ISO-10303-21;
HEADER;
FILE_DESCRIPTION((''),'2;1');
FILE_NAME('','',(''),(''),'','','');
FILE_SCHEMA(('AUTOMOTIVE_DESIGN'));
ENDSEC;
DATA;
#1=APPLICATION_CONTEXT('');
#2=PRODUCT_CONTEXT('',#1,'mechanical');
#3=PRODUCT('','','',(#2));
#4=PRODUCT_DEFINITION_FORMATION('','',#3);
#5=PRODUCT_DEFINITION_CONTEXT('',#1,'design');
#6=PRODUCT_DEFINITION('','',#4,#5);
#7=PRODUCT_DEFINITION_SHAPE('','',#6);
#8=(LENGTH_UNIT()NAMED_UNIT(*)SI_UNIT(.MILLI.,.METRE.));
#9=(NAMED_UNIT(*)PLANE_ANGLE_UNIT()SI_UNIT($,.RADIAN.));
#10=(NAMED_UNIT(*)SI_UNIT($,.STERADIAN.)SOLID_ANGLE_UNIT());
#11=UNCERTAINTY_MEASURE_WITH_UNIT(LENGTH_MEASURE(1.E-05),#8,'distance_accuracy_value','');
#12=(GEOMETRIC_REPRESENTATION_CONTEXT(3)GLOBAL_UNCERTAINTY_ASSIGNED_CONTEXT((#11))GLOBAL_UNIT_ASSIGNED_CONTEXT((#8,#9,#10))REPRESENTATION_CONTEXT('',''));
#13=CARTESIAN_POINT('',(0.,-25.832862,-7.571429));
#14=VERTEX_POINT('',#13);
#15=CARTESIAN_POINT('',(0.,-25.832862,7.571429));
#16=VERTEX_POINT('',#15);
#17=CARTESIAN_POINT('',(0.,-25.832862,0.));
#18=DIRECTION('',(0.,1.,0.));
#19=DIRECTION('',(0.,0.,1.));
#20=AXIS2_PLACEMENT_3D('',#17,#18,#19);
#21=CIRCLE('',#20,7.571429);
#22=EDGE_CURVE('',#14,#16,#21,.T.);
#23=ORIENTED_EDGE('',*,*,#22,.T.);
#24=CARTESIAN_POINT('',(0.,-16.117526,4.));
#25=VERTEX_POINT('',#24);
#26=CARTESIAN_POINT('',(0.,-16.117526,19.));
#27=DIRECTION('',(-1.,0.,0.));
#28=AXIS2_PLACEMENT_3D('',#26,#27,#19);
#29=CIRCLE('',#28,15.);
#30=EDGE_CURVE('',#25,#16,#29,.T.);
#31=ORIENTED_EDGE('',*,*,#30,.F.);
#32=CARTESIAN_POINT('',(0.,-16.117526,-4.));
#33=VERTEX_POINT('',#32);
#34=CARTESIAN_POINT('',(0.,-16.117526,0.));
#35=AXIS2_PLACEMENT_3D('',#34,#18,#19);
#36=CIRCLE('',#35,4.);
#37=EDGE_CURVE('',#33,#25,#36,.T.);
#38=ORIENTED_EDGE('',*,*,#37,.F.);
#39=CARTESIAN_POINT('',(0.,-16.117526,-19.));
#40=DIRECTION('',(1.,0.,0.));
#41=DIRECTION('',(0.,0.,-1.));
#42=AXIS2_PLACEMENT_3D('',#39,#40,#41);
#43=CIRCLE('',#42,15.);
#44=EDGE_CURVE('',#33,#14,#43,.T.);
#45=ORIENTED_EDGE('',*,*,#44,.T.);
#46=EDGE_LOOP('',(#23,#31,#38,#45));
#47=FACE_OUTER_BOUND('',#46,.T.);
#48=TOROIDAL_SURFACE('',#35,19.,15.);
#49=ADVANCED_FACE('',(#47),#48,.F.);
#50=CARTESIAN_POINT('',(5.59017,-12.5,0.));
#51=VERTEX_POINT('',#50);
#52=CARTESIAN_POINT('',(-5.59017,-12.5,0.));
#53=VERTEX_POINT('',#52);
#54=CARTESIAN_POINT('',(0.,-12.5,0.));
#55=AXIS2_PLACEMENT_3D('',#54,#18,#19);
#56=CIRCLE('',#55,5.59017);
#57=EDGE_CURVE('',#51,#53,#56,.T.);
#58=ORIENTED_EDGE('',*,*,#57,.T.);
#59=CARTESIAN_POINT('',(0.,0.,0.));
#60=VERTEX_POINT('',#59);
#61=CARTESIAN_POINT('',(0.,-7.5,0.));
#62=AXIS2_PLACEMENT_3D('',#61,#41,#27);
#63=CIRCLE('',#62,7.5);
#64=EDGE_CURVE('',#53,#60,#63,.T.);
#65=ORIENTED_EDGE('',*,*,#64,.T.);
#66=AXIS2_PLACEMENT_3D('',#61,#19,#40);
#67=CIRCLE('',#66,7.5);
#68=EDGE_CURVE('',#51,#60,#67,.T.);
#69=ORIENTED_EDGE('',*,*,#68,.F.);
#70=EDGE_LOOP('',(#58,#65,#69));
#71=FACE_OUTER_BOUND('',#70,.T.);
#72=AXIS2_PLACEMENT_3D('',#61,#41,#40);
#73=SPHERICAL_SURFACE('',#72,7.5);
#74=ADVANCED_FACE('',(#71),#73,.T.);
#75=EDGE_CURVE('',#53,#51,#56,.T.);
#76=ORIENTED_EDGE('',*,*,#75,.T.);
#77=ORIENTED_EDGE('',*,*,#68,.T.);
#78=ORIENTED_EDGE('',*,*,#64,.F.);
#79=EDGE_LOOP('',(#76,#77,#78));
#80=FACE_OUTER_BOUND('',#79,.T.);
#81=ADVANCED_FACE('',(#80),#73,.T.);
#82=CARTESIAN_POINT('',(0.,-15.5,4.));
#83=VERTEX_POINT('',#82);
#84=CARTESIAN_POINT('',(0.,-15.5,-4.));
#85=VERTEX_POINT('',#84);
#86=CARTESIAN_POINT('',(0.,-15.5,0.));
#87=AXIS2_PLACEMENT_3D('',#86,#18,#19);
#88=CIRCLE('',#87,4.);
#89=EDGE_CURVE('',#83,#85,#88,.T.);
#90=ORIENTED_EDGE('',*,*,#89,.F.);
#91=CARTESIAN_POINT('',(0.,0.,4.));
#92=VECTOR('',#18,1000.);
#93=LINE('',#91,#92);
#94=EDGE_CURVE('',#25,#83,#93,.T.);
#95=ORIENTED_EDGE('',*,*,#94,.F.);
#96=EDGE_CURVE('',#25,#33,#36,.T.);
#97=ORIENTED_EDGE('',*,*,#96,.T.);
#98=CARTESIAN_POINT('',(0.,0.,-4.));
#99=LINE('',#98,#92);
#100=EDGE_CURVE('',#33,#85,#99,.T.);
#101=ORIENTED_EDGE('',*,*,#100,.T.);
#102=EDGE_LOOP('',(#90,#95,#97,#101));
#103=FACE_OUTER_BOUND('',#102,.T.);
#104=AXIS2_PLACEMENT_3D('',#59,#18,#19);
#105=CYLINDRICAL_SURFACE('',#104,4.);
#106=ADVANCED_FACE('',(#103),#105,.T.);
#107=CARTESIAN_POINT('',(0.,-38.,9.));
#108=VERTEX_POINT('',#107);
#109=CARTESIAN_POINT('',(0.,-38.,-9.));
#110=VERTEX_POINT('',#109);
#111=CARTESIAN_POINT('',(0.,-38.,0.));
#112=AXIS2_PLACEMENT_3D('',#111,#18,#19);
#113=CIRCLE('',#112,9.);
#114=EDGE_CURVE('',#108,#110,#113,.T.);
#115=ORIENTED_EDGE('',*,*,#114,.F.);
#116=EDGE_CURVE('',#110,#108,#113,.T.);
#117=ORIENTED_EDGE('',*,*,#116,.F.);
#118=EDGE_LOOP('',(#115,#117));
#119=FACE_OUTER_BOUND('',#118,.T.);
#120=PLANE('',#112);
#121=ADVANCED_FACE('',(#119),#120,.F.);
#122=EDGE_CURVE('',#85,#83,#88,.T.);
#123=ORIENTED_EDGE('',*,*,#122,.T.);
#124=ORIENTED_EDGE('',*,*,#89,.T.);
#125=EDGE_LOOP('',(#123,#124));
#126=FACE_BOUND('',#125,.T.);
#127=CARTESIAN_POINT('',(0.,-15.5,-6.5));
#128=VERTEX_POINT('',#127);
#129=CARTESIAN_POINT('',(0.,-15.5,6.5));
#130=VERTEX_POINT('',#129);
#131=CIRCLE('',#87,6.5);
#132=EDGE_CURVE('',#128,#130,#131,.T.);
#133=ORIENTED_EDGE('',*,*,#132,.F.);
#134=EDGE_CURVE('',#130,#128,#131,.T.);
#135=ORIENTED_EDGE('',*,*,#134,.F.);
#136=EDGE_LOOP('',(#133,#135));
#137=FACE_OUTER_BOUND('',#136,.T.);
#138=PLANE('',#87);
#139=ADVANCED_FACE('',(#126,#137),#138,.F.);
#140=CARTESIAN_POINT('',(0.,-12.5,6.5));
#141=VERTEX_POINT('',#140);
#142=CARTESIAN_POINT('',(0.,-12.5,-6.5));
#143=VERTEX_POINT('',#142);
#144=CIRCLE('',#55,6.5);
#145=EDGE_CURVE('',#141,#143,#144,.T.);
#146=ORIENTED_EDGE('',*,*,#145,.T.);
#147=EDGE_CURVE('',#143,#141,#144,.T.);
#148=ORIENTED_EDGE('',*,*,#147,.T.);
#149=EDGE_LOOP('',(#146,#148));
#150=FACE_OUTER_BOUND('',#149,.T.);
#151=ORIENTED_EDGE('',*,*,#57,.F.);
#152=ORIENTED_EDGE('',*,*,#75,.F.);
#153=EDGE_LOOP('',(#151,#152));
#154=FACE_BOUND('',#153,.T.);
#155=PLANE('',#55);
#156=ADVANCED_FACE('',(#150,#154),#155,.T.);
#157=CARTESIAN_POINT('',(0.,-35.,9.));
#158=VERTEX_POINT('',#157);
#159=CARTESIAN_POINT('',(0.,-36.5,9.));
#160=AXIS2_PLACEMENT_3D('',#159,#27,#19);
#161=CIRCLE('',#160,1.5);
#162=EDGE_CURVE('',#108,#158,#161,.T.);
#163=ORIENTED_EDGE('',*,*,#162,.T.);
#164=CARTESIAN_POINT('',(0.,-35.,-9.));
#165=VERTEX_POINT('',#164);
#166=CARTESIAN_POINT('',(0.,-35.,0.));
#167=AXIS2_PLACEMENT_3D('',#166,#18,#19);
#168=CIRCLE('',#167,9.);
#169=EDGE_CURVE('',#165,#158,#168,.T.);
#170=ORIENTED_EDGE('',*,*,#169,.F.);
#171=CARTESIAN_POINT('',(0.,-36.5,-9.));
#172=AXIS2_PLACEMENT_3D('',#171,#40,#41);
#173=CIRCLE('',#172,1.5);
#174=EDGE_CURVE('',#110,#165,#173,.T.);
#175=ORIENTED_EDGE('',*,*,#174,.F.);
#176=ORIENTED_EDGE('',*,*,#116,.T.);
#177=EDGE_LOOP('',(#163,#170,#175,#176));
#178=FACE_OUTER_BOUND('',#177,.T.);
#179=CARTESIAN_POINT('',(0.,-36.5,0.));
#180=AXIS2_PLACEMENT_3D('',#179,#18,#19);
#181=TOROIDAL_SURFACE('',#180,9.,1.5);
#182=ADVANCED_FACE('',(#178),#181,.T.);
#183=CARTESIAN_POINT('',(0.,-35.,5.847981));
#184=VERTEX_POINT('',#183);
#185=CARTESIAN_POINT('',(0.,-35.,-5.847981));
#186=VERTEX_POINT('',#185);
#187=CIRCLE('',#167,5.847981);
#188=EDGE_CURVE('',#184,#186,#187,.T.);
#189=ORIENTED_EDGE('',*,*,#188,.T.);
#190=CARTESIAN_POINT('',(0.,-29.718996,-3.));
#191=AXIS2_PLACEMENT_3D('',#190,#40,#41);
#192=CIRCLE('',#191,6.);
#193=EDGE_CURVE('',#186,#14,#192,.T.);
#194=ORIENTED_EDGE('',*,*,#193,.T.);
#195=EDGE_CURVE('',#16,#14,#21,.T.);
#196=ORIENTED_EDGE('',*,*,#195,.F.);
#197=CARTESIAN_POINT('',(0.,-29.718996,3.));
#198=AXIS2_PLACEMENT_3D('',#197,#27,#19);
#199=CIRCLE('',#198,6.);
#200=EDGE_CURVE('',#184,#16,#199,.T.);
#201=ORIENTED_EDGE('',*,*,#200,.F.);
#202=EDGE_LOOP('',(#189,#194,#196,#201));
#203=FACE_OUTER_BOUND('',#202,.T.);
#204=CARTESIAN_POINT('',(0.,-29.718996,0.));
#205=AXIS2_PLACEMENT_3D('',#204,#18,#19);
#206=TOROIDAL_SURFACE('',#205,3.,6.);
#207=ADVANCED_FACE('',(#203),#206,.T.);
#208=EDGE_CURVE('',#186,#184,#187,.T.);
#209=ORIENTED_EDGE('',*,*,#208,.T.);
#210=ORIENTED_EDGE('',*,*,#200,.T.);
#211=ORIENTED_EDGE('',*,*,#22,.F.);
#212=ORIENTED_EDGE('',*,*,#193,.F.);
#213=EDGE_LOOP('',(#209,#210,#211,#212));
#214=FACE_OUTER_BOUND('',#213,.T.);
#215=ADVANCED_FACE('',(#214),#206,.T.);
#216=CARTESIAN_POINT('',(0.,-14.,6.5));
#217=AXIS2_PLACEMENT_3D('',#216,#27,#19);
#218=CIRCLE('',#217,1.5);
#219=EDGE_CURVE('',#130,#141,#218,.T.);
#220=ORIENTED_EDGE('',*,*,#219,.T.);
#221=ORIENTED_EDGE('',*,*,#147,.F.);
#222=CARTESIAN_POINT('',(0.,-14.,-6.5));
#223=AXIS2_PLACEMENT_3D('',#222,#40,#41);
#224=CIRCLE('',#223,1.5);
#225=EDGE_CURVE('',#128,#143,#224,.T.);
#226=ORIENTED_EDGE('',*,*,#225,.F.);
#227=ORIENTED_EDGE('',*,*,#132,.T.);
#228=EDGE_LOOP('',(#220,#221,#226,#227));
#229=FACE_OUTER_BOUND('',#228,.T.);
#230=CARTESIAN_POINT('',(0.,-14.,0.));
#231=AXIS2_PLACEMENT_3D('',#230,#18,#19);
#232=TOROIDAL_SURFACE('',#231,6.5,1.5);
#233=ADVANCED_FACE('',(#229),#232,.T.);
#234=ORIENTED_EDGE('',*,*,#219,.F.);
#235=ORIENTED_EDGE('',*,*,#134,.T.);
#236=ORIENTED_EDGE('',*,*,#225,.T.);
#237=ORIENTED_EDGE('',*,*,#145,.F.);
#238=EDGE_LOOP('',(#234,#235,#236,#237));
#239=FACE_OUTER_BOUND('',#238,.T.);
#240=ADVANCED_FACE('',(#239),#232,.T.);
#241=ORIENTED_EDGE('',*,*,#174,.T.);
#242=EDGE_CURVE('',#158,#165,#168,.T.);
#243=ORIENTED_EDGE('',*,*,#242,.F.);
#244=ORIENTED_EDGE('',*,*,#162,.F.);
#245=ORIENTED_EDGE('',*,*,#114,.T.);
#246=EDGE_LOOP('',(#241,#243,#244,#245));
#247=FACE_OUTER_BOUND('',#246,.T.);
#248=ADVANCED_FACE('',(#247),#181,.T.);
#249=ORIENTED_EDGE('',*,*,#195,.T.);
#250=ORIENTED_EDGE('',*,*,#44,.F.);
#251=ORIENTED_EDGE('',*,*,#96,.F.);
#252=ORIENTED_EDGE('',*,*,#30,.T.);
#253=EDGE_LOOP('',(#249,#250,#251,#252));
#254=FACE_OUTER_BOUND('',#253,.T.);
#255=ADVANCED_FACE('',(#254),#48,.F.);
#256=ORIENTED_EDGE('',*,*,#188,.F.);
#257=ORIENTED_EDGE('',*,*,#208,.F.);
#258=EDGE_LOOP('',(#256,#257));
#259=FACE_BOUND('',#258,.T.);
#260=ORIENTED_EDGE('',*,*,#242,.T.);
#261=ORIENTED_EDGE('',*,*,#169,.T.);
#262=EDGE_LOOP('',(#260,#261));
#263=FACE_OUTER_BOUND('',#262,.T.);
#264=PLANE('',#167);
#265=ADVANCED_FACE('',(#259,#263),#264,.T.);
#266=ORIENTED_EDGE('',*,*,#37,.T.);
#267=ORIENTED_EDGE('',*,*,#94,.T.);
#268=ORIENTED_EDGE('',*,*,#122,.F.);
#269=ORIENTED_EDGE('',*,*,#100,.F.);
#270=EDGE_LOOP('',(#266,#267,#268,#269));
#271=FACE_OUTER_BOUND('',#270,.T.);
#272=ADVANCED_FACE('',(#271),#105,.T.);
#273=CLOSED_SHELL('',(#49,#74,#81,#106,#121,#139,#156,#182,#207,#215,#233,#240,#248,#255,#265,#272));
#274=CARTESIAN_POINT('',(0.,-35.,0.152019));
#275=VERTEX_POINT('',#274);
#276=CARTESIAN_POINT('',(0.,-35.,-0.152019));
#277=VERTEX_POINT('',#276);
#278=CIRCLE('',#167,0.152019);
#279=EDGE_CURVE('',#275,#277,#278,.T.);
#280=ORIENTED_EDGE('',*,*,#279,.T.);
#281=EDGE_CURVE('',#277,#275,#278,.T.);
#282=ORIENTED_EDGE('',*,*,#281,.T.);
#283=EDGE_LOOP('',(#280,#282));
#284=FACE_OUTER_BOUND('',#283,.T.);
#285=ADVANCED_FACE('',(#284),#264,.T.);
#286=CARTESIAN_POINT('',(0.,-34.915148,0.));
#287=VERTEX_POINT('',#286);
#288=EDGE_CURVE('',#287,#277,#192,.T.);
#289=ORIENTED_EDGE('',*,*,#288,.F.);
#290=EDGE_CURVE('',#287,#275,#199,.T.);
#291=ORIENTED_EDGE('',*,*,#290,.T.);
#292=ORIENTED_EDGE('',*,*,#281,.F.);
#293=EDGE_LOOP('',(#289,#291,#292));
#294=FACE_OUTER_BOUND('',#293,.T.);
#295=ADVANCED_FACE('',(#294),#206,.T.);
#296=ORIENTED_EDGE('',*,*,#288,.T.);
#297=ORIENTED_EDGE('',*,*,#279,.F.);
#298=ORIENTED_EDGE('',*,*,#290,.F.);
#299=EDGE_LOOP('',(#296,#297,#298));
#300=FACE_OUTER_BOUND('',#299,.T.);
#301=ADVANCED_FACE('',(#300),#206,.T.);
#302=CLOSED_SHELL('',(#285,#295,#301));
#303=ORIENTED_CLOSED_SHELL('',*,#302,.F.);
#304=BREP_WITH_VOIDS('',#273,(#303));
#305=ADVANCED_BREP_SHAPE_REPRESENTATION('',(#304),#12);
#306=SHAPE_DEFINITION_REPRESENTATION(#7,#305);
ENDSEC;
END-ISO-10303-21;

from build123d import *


with BuildPart() as part:
    # Pawn Profile Sketch → Pawn Body Revolve (revolve)
    with BuildSketch(Plane.XY, mode=Mode.PRIVATE) as pawn_body_revolve_sk:
        with BuildLine():
            Line((0, -15.5), (0, -12.5))
            Line((0, -12.5), (-5.590169944, -12.5))
            Line((-5.590169944, -12.5), (-6.5, -12.5))
            ThreePointArc((-6.5, -12.5), (-8, -14), (-6.5, -15.5))
            Line((-6.5, -15.5), (-4, -15.5))
            Line((-4, -15.5), (0, -15.5))
        make_face()
        with BuildLine():
            Line((0, -12.5), (0, 0))
            ThreePointArc((0, 0), (-6.846531969, -4.438137822), (-5.590169944, -12.5))
            Line((-5.590169944, -12.5), (0, -12.5))
        make_face()
        with BuildLine():
            Line((0, -34.915148474), (0, -15.5))
            Line((0, -15.5), (-4, -15.5))
            Line((-4, -15.5), (-4, -16.117525543))
            ThreePointArc((-4, -16.117525543), (-4.921140468, -21.293017238), (-7.571428571, -25.83286162))
            ThreePointArc((-7.571428571, -25.83286162), (-8.896695439, -30.827591061), (-5.847981266, -35))
            Line((-5.847981266, -35), (-0.152018734, -35))
            ThreePointArc((-0.152018734, -35), (-0.075701594, -34.958125638), (0, -34.915148474))
        make_face()
        with BuildLine():
            Line((0, -38), (0, -35))
            Line((0, -35), (-0.152018734, -35))
            Line((-0.152018734, -35), (-5.847981266, -35))
            Line((-5.847981266, -35), (-9, -35))
            ThreePointArc((-9, -35), (-10.5, -36.5), (-9, -38))
            Line((-9, -38), (0, -38))
        make_face()
    revolve(pawn_body_revolve_sk.sketch.rotate(Axis((0, 0, 0), (0, -1, 0)), 270), axis=Axis((0, 0, 0), (0, -1, 0)))


solid = part.part
